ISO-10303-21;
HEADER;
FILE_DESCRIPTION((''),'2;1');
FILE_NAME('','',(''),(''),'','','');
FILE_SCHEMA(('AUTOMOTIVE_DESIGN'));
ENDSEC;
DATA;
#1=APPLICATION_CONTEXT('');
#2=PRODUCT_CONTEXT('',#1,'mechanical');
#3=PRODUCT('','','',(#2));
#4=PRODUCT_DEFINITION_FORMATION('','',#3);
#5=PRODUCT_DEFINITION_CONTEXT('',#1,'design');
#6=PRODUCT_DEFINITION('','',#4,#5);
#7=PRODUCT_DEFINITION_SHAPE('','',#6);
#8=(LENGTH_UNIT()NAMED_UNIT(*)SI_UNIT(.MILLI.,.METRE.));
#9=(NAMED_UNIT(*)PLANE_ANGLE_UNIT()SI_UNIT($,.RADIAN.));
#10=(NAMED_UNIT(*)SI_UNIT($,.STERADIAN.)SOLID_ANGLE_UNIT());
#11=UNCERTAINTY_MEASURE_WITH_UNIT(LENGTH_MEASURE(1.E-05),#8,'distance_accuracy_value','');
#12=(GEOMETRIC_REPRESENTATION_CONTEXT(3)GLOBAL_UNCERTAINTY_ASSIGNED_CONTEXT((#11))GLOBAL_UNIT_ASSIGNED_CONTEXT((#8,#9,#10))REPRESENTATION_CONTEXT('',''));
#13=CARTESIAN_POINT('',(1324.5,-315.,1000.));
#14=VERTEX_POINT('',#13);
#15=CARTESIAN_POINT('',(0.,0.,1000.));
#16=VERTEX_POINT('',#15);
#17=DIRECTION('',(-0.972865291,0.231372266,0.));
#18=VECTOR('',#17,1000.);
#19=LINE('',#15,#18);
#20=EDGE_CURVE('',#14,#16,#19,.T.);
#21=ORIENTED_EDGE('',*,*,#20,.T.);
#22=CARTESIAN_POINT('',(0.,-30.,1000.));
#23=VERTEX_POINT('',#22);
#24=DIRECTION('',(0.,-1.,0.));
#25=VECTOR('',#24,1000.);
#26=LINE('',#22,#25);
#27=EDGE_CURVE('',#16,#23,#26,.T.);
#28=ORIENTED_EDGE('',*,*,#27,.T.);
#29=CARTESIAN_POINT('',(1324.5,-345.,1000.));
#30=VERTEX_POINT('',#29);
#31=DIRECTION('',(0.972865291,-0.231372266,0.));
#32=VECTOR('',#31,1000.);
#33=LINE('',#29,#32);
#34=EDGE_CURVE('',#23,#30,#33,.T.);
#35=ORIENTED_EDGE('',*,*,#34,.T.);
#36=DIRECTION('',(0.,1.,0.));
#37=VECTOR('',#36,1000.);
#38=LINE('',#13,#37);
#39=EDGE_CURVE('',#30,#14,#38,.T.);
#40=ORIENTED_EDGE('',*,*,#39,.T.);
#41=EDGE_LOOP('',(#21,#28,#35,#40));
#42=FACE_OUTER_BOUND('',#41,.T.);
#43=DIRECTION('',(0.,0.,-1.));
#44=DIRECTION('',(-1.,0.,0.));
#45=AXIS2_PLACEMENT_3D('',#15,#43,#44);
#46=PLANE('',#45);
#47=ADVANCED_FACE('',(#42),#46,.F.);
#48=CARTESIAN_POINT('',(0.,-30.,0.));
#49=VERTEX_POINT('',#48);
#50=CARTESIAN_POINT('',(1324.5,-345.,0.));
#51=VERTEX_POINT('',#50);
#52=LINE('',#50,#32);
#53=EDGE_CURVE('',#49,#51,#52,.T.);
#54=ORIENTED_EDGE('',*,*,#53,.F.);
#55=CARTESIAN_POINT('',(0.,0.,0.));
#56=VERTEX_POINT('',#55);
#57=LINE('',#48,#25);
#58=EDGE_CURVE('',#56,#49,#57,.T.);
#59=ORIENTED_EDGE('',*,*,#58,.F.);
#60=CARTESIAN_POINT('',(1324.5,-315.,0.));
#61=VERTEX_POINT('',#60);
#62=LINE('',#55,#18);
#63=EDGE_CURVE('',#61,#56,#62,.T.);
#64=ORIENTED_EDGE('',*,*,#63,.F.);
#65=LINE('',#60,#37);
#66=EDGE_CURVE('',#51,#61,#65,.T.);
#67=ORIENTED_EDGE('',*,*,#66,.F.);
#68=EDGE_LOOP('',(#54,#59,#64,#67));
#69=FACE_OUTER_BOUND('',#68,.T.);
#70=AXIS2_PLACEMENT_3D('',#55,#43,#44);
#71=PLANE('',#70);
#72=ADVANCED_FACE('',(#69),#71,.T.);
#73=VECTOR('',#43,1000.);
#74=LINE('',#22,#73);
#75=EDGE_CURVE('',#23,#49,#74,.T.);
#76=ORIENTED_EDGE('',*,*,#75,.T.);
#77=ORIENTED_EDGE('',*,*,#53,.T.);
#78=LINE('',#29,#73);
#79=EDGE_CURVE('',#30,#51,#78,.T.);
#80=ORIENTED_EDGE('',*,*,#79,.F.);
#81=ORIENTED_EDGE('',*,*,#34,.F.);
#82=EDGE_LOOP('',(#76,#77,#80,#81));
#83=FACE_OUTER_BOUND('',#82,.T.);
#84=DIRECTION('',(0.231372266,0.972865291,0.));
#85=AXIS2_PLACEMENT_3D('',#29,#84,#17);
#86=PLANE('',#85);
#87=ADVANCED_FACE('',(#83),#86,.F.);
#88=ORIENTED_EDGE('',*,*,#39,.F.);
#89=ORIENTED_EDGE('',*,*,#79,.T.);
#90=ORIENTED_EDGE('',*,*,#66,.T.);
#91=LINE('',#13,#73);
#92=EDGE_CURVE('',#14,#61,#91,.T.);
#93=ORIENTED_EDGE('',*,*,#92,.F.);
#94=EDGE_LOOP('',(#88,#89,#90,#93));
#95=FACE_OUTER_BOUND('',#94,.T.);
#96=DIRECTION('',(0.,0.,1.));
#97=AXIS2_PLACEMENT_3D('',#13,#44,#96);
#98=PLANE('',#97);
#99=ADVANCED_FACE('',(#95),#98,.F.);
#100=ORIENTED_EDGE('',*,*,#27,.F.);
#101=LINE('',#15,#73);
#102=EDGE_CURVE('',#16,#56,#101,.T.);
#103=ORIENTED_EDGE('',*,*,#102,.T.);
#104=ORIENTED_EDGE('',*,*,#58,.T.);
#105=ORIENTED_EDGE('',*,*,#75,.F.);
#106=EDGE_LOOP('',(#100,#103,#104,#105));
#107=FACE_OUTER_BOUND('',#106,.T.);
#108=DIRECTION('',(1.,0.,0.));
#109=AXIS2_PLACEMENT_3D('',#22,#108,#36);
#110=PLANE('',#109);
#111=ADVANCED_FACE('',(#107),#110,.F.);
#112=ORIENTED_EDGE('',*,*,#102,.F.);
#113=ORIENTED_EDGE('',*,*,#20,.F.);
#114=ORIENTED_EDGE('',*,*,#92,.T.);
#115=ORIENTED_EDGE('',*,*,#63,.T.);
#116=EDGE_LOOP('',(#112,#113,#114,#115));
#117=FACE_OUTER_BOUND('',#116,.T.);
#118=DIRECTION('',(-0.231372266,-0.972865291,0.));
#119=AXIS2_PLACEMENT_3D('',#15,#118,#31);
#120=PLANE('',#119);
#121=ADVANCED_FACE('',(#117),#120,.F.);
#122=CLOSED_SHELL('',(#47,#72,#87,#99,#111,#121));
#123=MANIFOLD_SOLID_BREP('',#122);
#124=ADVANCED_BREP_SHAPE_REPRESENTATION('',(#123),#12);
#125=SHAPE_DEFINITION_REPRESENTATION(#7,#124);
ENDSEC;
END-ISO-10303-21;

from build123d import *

# Parameters (mm, degrees)
EXTRUDE_1_DEPTH = 1000


with BuildPart() as part:
    # 草图1 → 凸台-拉伸1 (new body)
    with BuildSketch(Plane.XY):
        Polygon((0, 0), (1324.500000007, -314.999999957), (1324.500000007, -344.999999957), (0, -30), align=None)
    extrude(amount=EXTRUDE_1_DEPTH)


solid = part.part
